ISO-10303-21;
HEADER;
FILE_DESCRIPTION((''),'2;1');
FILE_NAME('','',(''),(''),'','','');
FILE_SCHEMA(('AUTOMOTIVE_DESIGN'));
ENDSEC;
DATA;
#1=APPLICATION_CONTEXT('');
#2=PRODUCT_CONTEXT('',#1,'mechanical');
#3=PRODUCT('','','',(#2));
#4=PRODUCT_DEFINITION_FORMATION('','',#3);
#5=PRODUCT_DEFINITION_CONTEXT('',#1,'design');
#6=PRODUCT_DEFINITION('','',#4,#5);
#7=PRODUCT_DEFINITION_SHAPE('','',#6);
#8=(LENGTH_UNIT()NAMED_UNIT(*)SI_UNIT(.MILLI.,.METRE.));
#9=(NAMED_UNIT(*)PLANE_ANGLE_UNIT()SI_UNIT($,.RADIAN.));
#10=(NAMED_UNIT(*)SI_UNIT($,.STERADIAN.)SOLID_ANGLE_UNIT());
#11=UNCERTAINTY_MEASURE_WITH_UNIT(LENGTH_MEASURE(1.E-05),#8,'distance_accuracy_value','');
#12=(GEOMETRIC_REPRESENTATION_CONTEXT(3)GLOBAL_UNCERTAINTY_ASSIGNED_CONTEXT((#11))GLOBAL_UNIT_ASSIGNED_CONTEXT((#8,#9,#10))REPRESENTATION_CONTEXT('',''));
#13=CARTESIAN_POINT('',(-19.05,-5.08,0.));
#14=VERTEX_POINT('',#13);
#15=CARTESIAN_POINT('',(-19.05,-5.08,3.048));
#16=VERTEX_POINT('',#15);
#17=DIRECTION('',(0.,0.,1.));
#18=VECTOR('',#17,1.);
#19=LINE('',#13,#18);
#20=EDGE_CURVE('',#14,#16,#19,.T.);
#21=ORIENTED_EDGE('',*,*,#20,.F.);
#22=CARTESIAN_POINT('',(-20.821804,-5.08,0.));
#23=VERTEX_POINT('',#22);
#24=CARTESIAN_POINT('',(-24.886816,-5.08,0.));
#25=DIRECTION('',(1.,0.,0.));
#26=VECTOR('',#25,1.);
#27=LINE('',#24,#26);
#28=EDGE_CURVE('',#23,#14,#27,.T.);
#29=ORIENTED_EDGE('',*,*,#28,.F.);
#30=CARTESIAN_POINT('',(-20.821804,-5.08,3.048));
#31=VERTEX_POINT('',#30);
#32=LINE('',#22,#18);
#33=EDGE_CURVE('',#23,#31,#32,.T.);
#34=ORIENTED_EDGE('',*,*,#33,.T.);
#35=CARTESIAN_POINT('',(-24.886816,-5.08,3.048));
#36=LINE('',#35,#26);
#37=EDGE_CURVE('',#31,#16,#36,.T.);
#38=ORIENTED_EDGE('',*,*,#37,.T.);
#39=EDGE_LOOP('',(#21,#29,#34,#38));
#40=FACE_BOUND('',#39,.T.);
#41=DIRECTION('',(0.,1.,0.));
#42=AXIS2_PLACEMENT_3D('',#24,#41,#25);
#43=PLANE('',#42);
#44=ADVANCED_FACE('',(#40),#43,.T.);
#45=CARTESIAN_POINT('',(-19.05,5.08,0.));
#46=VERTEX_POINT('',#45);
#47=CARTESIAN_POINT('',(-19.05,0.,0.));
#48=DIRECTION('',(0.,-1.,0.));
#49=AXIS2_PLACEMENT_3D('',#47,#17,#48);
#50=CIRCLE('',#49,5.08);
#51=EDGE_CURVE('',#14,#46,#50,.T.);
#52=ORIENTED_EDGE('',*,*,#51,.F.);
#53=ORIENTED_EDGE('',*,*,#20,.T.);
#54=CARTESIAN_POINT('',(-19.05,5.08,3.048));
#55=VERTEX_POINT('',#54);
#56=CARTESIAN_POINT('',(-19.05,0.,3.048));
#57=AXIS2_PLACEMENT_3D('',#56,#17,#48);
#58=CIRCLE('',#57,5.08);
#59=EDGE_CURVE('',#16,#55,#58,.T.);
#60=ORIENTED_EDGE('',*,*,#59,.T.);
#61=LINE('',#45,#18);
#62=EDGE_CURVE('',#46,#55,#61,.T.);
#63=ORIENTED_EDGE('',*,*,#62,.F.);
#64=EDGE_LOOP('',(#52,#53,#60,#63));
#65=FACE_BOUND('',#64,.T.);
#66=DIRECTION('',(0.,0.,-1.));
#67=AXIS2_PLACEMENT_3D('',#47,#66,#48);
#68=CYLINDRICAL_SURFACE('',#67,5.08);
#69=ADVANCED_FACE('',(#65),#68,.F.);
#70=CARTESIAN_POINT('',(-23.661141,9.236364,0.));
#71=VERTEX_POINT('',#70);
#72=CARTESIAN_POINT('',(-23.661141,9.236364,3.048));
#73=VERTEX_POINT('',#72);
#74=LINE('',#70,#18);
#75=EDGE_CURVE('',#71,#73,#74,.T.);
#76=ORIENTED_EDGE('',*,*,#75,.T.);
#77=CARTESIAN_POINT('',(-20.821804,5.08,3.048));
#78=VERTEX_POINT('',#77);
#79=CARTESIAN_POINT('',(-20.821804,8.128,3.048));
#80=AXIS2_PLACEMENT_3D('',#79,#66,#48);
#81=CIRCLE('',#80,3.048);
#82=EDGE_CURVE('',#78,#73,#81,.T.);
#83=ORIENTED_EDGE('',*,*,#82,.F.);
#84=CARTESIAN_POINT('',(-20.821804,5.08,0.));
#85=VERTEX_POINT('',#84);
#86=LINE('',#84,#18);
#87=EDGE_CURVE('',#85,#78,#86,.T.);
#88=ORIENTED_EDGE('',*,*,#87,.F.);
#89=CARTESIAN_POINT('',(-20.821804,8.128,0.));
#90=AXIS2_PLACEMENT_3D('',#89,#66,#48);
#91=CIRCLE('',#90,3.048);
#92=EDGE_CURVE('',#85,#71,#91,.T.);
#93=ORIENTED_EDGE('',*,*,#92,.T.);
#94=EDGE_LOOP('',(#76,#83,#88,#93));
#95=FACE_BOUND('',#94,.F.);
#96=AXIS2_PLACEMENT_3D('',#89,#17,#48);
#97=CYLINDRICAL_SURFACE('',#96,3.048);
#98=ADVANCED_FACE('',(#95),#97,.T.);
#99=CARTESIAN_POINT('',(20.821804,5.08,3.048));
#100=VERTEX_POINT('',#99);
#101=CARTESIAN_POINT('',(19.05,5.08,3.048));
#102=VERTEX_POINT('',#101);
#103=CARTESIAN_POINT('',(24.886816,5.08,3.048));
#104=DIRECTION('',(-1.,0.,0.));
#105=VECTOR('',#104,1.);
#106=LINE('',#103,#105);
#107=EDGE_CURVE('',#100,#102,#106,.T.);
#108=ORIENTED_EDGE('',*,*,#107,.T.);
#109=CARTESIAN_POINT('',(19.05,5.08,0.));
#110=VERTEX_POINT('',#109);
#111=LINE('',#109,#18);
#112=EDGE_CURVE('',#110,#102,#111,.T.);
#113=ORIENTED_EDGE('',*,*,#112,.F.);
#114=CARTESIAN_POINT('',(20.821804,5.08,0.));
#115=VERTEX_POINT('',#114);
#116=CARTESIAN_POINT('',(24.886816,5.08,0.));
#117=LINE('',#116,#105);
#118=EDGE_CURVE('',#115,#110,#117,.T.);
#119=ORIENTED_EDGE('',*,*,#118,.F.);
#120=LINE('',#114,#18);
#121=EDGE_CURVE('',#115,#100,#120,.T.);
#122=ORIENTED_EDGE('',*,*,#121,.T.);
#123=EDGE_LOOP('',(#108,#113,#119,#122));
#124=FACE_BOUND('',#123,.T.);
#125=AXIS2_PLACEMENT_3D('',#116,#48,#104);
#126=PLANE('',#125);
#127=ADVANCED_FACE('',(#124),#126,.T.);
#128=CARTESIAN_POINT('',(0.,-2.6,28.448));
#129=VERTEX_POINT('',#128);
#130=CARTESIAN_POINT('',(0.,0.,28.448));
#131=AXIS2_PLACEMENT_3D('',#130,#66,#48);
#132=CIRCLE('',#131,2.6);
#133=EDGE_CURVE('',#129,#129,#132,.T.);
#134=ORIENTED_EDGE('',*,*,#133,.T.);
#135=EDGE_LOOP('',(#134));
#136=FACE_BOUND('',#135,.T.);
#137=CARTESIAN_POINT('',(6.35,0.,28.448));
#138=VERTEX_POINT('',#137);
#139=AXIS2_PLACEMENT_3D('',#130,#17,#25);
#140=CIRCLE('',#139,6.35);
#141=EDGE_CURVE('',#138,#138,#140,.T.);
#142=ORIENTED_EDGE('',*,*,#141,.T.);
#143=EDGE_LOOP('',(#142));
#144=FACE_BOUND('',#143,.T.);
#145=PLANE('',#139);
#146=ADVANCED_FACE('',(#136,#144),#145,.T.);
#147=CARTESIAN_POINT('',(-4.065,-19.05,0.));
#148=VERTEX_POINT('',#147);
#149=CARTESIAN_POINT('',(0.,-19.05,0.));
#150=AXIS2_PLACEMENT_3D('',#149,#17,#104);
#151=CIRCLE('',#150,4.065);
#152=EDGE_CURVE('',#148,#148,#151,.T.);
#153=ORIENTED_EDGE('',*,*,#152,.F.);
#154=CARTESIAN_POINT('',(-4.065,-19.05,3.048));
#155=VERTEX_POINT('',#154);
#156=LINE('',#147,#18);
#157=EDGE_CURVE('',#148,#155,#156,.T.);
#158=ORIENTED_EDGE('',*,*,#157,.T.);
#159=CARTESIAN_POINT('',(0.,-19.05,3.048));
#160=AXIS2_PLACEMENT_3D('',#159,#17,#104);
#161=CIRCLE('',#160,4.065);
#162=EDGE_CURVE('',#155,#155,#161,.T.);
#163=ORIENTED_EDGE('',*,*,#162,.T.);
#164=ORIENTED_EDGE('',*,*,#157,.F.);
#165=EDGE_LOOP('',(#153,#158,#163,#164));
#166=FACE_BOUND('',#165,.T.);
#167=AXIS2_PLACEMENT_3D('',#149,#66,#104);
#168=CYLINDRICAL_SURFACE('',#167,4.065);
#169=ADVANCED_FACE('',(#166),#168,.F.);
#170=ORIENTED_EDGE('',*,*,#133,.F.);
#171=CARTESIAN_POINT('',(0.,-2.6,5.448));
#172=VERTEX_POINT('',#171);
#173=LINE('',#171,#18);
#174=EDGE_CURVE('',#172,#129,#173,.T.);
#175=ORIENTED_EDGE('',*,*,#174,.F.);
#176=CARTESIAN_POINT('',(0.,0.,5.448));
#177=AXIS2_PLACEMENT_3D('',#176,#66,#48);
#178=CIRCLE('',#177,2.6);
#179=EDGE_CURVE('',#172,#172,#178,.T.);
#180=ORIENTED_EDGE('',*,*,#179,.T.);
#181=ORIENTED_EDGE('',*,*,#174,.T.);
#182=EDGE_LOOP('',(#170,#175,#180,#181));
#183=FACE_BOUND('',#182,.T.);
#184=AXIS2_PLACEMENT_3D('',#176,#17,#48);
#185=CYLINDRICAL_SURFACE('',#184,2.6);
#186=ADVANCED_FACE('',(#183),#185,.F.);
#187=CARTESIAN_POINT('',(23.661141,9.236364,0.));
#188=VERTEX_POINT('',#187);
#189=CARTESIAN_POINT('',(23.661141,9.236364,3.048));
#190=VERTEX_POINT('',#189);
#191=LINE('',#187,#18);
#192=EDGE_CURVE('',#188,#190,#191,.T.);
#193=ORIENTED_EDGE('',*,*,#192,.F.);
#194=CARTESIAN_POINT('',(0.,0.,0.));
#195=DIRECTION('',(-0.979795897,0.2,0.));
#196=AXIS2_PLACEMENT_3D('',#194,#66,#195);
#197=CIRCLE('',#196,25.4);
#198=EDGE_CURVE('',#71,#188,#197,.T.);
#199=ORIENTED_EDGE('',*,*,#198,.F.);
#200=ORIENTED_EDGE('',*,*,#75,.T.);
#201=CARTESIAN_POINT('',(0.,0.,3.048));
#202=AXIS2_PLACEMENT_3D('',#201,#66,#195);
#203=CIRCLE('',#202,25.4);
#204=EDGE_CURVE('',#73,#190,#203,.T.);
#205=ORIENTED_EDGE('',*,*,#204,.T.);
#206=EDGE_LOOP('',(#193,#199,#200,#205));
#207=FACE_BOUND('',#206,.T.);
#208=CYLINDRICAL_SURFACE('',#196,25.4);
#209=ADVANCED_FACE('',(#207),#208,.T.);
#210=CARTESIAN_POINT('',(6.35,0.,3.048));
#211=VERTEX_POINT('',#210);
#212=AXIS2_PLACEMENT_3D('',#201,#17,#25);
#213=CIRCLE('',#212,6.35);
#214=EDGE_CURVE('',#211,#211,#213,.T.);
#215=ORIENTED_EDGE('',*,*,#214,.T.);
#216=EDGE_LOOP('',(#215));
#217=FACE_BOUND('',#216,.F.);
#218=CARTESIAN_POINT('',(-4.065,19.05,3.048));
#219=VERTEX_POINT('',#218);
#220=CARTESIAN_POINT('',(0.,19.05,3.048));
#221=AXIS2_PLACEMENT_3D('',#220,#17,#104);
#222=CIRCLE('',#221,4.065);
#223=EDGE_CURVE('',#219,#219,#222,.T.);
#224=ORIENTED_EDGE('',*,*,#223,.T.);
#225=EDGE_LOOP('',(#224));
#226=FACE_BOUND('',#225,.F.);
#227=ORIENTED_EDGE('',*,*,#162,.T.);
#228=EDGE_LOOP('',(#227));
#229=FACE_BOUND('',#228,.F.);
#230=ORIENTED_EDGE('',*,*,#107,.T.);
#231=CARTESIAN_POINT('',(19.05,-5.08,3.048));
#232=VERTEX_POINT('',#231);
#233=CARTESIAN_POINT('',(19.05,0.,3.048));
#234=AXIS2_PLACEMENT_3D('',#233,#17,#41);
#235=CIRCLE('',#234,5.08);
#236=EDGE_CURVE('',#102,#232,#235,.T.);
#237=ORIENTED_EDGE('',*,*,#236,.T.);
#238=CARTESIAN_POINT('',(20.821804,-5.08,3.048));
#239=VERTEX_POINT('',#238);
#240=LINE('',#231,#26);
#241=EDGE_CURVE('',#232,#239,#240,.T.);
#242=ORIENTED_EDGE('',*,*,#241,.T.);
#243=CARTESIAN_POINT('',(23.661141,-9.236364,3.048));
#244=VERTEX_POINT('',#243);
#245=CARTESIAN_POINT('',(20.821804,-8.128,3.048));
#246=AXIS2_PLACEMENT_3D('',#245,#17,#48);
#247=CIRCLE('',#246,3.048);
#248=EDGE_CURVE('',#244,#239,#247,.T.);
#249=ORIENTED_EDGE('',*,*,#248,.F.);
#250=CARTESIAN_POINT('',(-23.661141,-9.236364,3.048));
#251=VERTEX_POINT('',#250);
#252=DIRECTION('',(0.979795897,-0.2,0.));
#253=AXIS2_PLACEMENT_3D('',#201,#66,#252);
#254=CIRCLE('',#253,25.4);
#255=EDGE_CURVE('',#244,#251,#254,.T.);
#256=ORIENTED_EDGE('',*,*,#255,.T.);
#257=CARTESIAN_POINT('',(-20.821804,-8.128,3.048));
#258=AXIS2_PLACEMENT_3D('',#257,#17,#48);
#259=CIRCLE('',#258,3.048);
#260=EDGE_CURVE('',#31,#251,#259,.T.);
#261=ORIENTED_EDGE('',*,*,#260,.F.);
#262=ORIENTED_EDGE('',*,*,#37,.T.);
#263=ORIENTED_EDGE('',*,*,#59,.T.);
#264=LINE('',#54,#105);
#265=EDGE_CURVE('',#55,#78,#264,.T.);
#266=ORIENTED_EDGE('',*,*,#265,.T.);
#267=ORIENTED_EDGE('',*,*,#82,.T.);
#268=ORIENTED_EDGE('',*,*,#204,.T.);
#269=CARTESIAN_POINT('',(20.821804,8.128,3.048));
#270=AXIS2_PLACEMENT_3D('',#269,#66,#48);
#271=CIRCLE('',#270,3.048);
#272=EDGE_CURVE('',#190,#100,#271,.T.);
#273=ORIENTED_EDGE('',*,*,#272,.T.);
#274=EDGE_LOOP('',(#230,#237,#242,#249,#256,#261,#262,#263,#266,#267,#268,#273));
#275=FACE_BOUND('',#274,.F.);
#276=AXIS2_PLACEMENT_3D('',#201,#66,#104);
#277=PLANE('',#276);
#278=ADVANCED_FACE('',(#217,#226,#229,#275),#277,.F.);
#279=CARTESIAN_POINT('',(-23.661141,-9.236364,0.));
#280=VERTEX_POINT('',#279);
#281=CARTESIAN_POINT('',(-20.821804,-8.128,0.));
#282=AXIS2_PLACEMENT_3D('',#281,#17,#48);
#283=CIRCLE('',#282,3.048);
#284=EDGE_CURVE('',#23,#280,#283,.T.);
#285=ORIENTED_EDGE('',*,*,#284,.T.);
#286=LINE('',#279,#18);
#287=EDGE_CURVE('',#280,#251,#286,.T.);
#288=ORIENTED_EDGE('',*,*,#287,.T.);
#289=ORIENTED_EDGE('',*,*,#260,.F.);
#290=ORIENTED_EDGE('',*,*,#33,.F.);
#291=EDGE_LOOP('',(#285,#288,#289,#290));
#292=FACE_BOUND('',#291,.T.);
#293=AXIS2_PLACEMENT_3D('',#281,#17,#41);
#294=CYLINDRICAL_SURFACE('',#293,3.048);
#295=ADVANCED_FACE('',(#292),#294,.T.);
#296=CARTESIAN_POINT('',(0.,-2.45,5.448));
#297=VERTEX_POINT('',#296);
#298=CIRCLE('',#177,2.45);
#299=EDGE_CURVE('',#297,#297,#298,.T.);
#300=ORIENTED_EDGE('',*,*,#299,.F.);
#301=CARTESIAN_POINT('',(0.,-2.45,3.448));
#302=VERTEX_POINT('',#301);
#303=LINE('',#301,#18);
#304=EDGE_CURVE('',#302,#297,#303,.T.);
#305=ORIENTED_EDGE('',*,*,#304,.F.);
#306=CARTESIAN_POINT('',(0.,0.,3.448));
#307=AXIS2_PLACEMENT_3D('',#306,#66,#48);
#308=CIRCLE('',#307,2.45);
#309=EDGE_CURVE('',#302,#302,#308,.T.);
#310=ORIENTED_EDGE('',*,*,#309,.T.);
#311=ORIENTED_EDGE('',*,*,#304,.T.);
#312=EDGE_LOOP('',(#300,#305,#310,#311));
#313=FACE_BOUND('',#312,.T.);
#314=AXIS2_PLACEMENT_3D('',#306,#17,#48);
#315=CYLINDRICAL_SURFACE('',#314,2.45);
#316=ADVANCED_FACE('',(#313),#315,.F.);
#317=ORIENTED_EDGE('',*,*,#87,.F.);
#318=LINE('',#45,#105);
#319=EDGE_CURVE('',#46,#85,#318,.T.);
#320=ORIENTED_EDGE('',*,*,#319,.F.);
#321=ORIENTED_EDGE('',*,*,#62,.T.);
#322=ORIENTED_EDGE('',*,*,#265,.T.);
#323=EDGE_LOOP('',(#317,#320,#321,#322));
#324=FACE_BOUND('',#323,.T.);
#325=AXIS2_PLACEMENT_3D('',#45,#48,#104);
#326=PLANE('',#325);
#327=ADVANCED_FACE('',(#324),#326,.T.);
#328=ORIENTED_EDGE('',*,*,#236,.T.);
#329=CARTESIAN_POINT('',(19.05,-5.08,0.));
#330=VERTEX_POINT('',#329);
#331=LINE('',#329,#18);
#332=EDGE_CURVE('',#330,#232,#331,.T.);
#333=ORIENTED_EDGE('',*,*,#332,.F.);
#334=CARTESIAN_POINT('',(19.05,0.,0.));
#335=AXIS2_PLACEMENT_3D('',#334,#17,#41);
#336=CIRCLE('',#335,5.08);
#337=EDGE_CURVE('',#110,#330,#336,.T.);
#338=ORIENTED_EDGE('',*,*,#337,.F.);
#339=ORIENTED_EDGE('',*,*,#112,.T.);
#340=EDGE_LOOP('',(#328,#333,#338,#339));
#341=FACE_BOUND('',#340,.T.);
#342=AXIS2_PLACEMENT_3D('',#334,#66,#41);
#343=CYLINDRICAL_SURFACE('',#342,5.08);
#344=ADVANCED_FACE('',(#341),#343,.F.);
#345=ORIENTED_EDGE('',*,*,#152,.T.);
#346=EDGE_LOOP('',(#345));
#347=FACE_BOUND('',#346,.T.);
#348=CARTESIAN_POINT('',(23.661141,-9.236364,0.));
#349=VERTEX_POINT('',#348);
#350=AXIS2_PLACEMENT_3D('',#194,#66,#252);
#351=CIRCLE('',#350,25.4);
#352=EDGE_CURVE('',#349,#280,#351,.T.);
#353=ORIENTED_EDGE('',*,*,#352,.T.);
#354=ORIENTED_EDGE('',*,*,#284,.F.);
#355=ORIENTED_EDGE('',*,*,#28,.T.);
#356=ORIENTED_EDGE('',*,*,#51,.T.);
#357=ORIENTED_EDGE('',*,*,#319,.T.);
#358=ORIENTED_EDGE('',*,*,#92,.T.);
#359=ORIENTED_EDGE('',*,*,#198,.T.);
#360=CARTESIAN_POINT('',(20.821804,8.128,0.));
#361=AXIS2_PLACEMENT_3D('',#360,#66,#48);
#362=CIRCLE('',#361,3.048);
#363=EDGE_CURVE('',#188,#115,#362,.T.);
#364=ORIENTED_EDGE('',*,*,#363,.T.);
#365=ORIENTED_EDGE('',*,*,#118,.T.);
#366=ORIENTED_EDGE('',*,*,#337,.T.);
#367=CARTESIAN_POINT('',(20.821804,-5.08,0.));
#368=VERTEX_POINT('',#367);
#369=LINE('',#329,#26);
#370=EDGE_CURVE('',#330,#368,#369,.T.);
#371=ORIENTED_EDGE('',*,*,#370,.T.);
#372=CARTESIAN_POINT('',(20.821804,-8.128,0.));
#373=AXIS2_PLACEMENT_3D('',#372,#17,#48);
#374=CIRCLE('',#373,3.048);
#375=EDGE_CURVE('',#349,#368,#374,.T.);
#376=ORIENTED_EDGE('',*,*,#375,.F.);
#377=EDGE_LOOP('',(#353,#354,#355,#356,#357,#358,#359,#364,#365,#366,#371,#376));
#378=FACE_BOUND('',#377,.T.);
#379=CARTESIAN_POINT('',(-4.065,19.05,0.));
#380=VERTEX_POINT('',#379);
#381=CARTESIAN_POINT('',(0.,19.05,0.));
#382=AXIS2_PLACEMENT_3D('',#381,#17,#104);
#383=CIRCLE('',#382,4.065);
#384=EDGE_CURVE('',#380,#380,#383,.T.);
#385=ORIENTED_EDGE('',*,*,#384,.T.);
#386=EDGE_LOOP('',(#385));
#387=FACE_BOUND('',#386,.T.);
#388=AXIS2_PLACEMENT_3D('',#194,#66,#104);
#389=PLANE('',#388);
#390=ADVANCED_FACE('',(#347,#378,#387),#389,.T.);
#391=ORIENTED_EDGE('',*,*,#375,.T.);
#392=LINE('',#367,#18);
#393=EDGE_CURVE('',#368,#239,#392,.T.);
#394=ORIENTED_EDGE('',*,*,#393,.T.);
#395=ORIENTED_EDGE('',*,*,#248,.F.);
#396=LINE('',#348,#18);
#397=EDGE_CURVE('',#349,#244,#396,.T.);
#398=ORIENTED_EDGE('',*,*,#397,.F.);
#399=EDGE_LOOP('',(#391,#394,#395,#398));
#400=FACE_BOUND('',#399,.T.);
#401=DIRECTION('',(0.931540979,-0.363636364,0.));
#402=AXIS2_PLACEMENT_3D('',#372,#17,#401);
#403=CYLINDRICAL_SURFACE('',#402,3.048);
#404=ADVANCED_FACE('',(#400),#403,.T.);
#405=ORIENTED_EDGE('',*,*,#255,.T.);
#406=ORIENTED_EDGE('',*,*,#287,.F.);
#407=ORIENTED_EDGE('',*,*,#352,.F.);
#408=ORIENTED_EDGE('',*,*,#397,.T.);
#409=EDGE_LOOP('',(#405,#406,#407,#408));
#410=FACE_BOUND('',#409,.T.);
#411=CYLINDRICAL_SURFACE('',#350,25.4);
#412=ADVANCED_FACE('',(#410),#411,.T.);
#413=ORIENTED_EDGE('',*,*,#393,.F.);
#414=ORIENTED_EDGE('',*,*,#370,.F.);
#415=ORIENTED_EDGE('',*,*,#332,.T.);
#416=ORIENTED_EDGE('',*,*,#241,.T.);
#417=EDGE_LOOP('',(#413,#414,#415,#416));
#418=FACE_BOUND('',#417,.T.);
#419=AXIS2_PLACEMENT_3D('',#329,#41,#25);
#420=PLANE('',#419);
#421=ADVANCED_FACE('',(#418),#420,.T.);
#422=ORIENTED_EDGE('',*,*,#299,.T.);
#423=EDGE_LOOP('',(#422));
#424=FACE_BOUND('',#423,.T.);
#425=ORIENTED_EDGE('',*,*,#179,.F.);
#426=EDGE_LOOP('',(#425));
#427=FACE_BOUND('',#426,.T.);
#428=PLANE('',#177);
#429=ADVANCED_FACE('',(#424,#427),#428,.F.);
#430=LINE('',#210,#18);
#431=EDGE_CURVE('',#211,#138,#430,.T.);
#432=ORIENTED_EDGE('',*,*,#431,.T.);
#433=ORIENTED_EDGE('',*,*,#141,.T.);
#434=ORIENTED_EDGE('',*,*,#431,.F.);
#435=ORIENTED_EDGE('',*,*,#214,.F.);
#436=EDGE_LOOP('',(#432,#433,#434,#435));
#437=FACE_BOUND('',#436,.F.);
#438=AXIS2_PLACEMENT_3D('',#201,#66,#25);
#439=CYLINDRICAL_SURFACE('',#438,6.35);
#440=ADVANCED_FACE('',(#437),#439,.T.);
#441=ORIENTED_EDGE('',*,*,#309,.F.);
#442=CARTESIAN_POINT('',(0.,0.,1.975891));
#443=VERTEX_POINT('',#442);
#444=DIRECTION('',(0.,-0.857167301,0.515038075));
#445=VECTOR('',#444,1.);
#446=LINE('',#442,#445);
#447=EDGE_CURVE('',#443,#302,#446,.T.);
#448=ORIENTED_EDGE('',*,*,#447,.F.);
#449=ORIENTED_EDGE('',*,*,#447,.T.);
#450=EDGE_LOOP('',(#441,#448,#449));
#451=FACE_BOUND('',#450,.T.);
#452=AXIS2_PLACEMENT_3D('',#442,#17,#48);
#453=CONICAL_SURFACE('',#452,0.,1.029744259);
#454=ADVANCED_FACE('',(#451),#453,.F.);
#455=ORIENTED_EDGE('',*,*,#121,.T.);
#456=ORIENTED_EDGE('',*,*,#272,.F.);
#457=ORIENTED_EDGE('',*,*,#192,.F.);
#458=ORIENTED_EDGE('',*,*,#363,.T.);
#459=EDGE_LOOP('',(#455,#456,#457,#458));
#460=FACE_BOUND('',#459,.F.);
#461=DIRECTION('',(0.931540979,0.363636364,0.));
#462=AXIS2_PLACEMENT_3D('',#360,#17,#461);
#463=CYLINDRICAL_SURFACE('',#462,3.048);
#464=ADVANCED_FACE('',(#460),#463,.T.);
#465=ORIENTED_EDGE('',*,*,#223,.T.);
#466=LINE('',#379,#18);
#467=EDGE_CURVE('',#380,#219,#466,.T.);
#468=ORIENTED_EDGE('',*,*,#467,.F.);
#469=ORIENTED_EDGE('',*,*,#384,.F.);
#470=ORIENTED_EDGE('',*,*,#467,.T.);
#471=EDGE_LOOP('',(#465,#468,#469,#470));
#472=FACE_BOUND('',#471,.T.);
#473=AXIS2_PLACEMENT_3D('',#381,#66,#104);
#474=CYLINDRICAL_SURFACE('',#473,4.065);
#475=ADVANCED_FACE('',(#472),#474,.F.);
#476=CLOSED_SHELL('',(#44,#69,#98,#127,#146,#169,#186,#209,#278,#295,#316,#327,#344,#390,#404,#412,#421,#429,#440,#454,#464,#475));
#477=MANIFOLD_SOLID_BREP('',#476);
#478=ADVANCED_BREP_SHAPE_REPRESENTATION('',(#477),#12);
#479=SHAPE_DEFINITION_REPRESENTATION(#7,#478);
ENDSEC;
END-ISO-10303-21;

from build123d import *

# Parameters (mm, degrees)
PLATE_PROFILE_SKETCH_R    = 4.065
BASE_PLATE_0_12IN_DEPTH   = 3.048
PLATE_EDGE_FILLET_R0_12_R = 3.048
HUB_SKETCH_0_5_R          = 6.35
HUB_0_5_X_1IN_DEPTH       = 25.4


with BuildPart() as part:
    # Plate Profile Sketch → Base Plate 0.12in (new body)
    with BuildSketch(Plane.XY):
        with BuildLine():
            Line((-19.05, 5.08), (-24.886815787, 5.08))
            ThreePointArc((-24.886815787, 5.08), (0, 25.4), (24.886815787, 5.08))
            Line((24.886815787, 5.08), (19.05, 5.08))
            ThreePointArc((19.05, 5.08), (13.97, 0), (19.05, -5.08))
            Line((19.05, -5.08), (24.886815787, -5.08))
            ThreePointArc((24.886815787, -5.08), (0, -25.4), (-24.886815787, -5.08))
            Line((-24.886815787, -5.08), (-19.05, -5.08))
            ThreePointArc((-19.05, -5.08), (-13.97, 0), (-19.05, 5.08))
        make_face()
        with Locations(Location((0, 19.05, 0), (0, 0, 180))):
            Circle(PLATE_PROFILE_SKETCH_R, mode=Mode.SUBTRACT)
        with Locations(Location((0, -19.05, 0), (0, 0, 180))):
            Circle(PLATE_PROFILE_SKETCH_R, mode=Mode.SUBTRACT)
    extrude(amount=BASE_PLATE_0_12IN_DEPTH)

    # Plate Edge Fillet R0.12
    plate_edge_fillet_r0_12_edges = [part.edges().sort_by_distance(p)[0] for p in [
        (-24.886815787, 5.08, 1.524),
        (24.886815787, 5.08, 1.524),
        (24.886815787, -5.08, 1.524),
        (-24.886815787, -5.08, 1.524),
    ]]
    fillet(plate_edge_fillet_r0_12_edges, radius=PLATE_EDGE_FILLET_R0_12_R)

    # Hub Sketch Ø0.5 → Hub Ø0.5 x 1in (add)
    with BuildSketch(Plane.XY.offset(3.048)):
        Circle(HUB_SKETCH_0_5_R)
    extrude(amount=HUB_0_5_X_1IN_DEPTH)

    # Sketch5 → Hub Tapped Hole #10-24 (revolve, cut)
    with BuildSketch(Plane(origin=(0, 0, 28.448), x_dir=(0, -1, 0), z_dir=(1, 0, 0))):
        Polygon((0, 0), (0, 26.472108517), (2.45, 25), (2.45, 23), (2.6, 23), (2.6, 0), align=None)
    revolve(axis=Axis((0, 0, 34.798), (0, 0, -1)), mode=Mode.SUBTRACT)


solid = part.part
